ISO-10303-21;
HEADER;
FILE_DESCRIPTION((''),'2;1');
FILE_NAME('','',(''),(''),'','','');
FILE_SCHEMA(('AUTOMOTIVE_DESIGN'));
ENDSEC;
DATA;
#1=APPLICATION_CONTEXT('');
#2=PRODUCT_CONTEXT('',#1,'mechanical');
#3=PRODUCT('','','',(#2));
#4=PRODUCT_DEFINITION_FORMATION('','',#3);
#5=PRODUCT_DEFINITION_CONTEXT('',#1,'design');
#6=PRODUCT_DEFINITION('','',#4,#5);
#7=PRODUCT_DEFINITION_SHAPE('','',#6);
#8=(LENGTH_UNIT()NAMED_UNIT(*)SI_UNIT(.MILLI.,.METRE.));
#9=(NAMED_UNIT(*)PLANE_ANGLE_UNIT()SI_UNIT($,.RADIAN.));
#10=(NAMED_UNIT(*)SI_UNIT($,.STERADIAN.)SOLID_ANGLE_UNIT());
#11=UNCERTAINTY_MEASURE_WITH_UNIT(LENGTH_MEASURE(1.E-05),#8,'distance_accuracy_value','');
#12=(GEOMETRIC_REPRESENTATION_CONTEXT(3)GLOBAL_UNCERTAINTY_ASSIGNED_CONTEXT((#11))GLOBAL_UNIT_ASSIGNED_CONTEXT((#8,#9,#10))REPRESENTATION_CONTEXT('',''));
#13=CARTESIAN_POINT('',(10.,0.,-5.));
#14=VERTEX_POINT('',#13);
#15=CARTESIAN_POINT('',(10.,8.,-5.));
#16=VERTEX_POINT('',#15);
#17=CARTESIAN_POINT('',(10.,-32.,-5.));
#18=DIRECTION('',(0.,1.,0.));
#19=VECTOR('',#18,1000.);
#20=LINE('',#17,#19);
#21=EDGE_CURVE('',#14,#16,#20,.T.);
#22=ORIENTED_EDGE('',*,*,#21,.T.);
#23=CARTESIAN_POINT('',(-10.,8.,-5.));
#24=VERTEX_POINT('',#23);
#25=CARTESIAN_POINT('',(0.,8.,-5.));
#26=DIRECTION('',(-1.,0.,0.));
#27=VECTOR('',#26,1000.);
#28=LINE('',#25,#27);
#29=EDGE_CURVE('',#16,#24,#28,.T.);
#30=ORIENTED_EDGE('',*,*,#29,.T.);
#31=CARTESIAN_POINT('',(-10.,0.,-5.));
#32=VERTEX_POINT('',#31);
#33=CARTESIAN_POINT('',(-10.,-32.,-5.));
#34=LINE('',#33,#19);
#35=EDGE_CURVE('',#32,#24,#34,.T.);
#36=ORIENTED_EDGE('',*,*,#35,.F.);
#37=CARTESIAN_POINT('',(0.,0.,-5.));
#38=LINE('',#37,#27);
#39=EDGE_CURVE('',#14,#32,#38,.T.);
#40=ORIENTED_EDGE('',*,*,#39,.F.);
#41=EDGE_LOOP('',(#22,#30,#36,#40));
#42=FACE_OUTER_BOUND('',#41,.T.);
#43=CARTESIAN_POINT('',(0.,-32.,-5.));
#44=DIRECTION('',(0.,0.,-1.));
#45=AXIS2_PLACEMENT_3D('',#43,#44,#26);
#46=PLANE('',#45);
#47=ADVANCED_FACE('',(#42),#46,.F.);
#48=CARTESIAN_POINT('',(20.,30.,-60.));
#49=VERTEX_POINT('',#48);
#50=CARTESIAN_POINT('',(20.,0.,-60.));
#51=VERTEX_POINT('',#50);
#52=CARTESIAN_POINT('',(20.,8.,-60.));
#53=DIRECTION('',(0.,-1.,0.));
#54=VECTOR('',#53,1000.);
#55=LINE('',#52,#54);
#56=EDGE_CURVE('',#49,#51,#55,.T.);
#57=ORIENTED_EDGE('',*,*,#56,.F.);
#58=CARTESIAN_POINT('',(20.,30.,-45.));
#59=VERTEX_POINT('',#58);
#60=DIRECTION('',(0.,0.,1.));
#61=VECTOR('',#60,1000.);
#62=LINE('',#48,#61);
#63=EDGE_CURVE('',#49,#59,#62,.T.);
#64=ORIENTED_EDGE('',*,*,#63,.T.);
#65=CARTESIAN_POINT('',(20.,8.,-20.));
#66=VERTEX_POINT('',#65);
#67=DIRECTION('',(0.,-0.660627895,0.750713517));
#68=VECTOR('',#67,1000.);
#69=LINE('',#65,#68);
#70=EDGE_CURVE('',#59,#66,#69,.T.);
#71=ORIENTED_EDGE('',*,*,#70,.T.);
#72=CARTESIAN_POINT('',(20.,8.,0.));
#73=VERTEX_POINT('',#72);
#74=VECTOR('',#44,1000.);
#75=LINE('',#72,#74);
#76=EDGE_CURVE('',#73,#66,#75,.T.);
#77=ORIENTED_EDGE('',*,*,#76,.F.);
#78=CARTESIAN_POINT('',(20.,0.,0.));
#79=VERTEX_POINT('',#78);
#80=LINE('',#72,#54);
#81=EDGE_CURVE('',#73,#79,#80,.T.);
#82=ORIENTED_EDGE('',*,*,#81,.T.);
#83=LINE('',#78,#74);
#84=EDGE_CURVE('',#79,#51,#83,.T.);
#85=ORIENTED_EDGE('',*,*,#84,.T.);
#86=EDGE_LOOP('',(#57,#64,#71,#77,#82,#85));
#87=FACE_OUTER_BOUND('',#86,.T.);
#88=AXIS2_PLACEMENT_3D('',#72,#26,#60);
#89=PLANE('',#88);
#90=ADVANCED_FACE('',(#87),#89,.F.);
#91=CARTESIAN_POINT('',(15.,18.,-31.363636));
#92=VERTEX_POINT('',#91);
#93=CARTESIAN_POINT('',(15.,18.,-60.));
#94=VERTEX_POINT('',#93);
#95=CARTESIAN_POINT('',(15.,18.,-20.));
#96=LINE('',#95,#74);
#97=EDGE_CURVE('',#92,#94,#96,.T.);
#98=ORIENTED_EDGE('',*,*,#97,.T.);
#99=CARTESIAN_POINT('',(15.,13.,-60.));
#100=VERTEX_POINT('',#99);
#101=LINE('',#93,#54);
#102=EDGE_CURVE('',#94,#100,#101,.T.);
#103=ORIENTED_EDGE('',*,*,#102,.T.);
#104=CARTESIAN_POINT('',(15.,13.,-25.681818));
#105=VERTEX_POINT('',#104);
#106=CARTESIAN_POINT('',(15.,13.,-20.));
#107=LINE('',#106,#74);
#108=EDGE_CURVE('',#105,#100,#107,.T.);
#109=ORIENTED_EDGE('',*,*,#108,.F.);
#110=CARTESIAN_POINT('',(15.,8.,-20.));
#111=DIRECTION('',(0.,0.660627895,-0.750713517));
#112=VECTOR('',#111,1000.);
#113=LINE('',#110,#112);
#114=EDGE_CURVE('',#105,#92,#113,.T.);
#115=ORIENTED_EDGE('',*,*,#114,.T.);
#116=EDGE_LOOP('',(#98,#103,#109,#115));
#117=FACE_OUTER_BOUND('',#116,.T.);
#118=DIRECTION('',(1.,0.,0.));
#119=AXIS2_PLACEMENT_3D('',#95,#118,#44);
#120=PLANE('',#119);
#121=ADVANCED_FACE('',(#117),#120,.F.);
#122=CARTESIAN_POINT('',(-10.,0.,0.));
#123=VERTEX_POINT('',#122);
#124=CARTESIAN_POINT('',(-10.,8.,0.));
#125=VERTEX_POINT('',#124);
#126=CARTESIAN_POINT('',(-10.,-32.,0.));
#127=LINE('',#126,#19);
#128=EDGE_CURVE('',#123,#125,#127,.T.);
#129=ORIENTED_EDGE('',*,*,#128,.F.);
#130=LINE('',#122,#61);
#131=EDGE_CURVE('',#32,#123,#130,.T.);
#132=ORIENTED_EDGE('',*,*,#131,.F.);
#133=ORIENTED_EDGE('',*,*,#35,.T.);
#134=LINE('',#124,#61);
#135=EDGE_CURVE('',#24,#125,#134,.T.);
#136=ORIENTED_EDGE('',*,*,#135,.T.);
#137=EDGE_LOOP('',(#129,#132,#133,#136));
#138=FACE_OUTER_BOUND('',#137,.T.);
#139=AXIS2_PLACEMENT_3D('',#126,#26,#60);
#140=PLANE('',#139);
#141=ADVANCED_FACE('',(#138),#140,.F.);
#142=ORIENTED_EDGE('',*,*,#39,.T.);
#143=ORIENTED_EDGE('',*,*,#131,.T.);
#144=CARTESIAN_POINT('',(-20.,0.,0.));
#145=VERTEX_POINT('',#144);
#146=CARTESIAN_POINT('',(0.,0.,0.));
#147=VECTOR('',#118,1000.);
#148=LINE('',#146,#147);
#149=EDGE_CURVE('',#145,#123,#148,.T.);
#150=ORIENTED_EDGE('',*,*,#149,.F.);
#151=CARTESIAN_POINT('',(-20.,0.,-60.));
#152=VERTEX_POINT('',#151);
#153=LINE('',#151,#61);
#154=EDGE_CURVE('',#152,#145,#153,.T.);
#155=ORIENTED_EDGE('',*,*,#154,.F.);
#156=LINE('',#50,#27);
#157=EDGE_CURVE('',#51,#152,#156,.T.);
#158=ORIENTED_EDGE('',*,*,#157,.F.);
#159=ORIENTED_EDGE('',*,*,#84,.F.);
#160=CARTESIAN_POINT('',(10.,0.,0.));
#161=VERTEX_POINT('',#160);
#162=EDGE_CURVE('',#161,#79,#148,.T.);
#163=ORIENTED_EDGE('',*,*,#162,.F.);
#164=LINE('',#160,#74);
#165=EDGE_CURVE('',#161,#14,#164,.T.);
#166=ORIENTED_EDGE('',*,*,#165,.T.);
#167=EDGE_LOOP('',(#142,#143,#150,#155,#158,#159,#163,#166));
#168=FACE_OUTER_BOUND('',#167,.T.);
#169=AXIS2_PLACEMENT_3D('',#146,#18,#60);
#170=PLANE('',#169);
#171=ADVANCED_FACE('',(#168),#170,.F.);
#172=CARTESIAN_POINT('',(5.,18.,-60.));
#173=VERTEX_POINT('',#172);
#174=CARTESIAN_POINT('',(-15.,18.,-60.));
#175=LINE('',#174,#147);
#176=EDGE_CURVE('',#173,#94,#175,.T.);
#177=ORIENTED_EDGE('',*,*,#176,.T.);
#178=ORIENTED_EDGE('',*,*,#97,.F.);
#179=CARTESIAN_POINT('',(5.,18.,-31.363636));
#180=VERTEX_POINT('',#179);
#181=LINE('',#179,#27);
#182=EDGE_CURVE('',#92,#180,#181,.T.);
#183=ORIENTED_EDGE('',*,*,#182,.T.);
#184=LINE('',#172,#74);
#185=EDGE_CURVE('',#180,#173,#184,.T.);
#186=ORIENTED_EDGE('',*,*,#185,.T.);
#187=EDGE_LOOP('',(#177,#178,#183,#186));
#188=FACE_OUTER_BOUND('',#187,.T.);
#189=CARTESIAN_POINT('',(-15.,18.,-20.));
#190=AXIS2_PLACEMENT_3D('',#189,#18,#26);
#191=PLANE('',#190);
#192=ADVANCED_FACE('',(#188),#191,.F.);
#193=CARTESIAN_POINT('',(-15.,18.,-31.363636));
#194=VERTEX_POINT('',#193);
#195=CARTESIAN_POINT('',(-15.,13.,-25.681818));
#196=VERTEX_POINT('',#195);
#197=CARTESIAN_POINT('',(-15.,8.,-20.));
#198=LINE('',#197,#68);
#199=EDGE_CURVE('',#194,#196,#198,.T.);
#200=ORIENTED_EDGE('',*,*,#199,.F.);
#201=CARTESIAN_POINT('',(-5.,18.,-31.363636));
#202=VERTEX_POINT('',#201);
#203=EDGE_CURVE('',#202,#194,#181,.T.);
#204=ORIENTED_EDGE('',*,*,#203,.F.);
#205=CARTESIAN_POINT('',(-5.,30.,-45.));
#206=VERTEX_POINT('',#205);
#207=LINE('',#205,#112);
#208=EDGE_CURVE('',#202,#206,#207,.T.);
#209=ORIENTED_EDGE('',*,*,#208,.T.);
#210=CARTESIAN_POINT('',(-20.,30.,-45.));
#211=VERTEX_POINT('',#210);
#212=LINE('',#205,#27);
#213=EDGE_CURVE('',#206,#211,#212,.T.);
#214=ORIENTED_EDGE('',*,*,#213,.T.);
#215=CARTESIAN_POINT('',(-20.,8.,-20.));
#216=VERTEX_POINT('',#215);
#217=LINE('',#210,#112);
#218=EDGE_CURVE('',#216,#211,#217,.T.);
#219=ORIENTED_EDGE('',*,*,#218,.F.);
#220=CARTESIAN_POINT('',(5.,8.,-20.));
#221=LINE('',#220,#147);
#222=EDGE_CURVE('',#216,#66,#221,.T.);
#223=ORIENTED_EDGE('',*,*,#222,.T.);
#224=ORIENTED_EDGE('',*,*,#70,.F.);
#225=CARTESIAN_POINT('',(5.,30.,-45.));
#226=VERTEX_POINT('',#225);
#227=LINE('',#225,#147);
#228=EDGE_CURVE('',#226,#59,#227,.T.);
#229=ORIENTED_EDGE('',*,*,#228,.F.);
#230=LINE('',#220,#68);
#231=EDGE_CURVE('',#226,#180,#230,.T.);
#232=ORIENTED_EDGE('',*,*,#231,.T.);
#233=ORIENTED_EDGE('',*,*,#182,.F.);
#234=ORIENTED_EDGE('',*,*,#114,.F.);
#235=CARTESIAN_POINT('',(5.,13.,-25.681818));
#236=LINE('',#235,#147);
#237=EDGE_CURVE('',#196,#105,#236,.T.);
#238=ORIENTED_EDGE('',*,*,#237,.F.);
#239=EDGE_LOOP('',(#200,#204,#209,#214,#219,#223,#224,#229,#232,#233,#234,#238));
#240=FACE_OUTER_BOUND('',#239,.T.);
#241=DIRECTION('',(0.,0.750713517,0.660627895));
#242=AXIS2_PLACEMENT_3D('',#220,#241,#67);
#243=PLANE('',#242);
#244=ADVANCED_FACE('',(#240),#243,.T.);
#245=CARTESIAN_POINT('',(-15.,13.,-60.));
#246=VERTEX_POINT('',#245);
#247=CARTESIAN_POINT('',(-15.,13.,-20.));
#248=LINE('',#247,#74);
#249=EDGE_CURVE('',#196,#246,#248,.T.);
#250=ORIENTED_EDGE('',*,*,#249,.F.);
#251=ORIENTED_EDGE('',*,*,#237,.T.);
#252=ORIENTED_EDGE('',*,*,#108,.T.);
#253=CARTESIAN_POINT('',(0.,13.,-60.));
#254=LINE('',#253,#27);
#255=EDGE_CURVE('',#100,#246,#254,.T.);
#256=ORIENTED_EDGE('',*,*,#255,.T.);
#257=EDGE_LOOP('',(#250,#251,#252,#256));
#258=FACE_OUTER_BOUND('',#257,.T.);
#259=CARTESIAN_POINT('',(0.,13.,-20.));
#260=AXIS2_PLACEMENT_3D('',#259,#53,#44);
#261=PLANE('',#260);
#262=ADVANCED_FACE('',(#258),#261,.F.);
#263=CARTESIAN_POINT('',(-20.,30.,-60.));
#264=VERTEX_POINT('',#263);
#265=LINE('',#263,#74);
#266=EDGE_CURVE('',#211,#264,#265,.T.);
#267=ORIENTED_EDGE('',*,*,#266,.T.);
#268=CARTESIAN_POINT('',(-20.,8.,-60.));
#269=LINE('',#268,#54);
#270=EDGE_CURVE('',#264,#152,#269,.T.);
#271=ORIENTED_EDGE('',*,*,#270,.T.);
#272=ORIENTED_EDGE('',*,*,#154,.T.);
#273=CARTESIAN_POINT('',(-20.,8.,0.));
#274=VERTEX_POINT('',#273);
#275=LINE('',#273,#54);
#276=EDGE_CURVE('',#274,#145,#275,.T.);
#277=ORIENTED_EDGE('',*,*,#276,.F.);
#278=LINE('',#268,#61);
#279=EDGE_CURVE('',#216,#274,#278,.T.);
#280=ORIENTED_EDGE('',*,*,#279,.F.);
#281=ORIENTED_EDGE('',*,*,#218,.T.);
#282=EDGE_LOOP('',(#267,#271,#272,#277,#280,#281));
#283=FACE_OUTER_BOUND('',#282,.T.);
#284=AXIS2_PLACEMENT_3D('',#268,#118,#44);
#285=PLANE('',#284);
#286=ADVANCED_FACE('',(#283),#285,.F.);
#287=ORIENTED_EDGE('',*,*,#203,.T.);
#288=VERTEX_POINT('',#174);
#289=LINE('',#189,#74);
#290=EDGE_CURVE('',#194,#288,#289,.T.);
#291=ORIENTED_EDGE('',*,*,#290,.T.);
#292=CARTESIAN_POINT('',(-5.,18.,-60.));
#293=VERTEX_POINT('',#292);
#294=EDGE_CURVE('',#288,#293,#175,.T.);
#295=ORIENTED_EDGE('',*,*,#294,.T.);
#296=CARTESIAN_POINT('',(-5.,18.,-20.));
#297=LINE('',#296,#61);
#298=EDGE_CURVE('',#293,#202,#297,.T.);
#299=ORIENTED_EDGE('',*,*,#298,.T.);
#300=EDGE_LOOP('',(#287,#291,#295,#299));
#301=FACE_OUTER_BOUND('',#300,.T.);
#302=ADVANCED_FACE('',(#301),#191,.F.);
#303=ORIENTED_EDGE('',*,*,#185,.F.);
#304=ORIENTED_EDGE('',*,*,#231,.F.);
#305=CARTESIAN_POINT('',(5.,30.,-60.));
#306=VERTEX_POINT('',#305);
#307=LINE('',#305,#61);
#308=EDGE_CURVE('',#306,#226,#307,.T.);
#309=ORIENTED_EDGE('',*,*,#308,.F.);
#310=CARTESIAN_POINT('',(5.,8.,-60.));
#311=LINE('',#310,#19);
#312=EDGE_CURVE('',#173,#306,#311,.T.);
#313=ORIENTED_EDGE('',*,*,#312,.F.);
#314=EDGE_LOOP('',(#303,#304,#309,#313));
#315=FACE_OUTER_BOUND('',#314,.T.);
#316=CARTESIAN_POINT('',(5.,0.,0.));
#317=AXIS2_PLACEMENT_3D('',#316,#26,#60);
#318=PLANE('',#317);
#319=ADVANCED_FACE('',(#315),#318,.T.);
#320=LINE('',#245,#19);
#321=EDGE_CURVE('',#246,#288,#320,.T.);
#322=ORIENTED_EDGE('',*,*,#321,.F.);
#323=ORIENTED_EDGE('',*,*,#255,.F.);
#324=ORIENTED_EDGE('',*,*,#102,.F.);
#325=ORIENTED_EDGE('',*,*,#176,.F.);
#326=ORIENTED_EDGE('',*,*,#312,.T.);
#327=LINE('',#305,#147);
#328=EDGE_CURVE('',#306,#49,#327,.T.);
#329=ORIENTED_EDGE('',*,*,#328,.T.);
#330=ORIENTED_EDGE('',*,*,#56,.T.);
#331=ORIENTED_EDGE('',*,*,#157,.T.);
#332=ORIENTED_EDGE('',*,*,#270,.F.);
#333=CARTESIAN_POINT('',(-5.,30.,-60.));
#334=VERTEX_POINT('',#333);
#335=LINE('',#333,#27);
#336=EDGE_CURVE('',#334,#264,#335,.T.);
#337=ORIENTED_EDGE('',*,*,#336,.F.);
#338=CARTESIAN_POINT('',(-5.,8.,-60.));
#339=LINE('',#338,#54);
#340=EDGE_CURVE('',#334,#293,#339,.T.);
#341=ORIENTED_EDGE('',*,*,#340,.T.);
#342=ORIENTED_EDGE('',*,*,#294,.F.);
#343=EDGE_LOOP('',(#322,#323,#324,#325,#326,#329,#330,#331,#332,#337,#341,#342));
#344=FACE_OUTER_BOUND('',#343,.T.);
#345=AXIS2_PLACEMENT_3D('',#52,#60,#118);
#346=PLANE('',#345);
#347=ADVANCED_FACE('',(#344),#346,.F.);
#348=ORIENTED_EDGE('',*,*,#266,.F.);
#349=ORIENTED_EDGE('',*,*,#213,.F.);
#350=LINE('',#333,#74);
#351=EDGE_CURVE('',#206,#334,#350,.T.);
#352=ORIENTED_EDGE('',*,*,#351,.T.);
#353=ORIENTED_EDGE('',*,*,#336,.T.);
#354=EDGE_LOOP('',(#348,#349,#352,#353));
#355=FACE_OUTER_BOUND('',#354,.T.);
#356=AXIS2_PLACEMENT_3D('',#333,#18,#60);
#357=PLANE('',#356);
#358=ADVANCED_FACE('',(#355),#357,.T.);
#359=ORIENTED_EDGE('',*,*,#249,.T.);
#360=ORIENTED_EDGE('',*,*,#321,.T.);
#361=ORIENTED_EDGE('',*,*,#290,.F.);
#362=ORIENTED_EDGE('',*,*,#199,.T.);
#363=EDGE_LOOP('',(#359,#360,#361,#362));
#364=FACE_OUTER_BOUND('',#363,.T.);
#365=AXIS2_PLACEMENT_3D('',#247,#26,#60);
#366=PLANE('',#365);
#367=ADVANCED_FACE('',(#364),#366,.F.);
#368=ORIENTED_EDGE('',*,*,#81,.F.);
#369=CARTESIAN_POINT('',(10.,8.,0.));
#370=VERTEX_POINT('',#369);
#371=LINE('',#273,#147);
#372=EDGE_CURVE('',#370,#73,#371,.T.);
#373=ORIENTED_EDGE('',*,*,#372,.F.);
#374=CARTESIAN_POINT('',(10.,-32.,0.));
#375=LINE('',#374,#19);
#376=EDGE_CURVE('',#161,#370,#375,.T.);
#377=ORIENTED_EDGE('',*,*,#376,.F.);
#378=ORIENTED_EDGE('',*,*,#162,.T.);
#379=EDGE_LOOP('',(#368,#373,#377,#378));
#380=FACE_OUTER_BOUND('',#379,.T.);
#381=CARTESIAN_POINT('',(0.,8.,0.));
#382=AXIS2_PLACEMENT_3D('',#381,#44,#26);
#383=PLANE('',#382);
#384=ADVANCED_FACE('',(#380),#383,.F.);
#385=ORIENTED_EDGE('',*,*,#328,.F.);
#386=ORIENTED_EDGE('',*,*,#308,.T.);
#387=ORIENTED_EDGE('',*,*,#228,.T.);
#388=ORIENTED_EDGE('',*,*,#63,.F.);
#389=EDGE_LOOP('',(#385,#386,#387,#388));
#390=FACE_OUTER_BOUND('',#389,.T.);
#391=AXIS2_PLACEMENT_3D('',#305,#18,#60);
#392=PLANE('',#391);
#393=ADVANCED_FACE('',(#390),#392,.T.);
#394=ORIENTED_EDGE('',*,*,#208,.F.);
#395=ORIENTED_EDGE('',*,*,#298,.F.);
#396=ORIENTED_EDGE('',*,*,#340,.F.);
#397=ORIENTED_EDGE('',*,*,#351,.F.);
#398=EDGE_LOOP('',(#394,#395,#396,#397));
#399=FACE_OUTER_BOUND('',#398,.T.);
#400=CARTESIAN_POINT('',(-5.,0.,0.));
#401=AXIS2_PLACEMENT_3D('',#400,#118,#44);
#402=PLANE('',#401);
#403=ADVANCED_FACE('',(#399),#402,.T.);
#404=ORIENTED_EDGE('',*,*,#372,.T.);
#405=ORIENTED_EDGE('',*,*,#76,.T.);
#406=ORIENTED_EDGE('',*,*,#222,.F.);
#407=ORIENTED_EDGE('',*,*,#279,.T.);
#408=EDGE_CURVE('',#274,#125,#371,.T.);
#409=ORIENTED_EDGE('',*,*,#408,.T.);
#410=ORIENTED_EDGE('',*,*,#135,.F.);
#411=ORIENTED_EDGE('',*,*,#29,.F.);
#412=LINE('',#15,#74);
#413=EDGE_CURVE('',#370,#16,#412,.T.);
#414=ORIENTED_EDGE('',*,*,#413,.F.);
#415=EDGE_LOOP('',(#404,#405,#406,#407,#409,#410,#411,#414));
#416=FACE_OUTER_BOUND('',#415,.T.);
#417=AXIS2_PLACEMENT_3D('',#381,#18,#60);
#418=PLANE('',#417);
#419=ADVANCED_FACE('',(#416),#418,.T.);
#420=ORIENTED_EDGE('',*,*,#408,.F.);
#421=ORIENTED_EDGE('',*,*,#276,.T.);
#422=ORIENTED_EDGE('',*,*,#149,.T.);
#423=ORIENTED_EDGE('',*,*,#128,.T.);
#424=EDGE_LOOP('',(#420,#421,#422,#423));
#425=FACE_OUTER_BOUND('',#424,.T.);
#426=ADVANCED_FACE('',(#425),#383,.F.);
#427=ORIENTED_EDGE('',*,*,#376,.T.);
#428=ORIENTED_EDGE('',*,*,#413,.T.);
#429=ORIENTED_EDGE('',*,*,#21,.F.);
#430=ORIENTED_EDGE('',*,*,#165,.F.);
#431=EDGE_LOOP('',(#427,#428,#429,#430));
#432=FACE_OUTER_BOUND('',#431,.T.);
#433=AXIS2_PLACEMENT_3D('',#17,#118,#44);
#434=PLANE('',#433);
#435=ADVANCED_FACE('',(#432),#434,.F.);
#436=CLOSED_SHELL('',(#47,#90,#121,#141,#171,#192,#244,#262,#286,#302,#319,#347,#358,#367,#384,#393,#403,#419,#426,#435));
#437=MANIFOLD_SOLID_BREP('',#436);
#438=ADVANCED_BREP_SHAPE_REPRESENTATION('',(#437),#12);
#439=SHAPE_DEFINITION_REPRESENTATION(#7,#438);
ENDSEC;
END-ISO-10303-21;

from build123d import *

# Parameters (mm, degrees)
BASE_PLATE_8MM_DEPTH      = 8
UPRIGHT_LOWER_15MM_DEPTH  = 15
UPRIGHT_MIDDLE_15MM_DEPTH = 15
UPRIGHT_TOP_SKETCH_W      = 10
UPRIGHT_TOP_SKETCH_H      = 40
UPRIGHT_TOP_10MM_DEPTH    = 10
SLOPE_CUT_DEPTH           = 40
CENTRE_SLOT_CUT_DEPTH     = 40
FRONT_NOTCH_CUT_DEPTH     = 40


with BuildPart() as part:
    # Base Plate Sketch → Base Plate 8mm (new body)
    with BuildSketch(Plane(origin=(0, 0, 0), x_dir=(1, 0, 0), z_dir=(0, 1, 0))):
        Polygon((0, 0), (20, 0), (20, 60), (-20, 60), (-20, 0), align=None)
    extrude(amount=BASE_PLATE_8MM_DEPTH)

    # Upright Lower Sketch → Upright Lower 15mm (add)
    with BuildSketch(Plane(origin=(20, 0, 0), x_dir=(0, 0, -1), z_dir=(1, 0, 0))):
        Polygon((60, 8), (60, 30), (45, 30), (20, 8), align=None)
    extrude(amount=-UPRIGHT_LOWER_15MM_DEPTH)

    # Upright Middle Sketch → Upright Middle 15mm (add)
    with BuildSketch(Plane.ZY.offset(20)):
        Polygon((-60, 8), (-60, 30), (-45, 30), (-20, 8), align=None)
    extrude(amount=-UPRIGHT_MIDDLE_15MM_DEPTH)

    # Upright Top Sketch → Upright Top 10mm (add)
    with BuildSketch(Plane(origin=(0, 8, 0), x_dir=(1, 0, 0), z_dir=(0, 1, 0))):
        with Locations((0, 40)):
            Rectangle(UPRIGHT_TOP_SKETCH_W, UPRIGHT_TOP_SKETCH_H)
    extrude(amount=UPRIGHT_TOP_10MM_DEPTH)

    # Slope Cut Sketch → Slope Cut (cut)
    with BuildSketch(Plane(origin=(5, 0, 0), x_dir=(0, 0, -1), z_dir=(1, 0, 0))):
        Polygon((20, 8), (20, 18), (31.363636364, 18), align=None)
    extrude(amount=-SLOPE_CUT_DEPTH, mode=Mode.SUBTRACT)

    # Centre Slot Sketch → Centre Slot Cut (cut)
    with BuildSketch(Plane(origin=(0, 0, -60), x_dir=(-1, 0, 0), z_dir=(0, 0, -1))):
        Polygon((0, 13), (15, 13), (15, 18), (-15, 18), (-15, 13), align=None)
    extrude(amount=-CENTRE_SLOT_CUT_DEPTH, mode=Mode.SUBTRACT)

    # Front Notch Sketch → Front Notch Cut (cut)
    with BuildSketch(Plane(origin=(0, 8, 0), x_dir=(1, 0, 0), z_dir=(0, 1, 0))):
        Polygon((0, 5), (10, 5), (10, 0), (-10, 0), (-10, 5), align=None)
    extrude(amount=-FRONT_NOTCH_CUT_DEPTH, mode=Mode.SUBTRACT)


solid = part.part
